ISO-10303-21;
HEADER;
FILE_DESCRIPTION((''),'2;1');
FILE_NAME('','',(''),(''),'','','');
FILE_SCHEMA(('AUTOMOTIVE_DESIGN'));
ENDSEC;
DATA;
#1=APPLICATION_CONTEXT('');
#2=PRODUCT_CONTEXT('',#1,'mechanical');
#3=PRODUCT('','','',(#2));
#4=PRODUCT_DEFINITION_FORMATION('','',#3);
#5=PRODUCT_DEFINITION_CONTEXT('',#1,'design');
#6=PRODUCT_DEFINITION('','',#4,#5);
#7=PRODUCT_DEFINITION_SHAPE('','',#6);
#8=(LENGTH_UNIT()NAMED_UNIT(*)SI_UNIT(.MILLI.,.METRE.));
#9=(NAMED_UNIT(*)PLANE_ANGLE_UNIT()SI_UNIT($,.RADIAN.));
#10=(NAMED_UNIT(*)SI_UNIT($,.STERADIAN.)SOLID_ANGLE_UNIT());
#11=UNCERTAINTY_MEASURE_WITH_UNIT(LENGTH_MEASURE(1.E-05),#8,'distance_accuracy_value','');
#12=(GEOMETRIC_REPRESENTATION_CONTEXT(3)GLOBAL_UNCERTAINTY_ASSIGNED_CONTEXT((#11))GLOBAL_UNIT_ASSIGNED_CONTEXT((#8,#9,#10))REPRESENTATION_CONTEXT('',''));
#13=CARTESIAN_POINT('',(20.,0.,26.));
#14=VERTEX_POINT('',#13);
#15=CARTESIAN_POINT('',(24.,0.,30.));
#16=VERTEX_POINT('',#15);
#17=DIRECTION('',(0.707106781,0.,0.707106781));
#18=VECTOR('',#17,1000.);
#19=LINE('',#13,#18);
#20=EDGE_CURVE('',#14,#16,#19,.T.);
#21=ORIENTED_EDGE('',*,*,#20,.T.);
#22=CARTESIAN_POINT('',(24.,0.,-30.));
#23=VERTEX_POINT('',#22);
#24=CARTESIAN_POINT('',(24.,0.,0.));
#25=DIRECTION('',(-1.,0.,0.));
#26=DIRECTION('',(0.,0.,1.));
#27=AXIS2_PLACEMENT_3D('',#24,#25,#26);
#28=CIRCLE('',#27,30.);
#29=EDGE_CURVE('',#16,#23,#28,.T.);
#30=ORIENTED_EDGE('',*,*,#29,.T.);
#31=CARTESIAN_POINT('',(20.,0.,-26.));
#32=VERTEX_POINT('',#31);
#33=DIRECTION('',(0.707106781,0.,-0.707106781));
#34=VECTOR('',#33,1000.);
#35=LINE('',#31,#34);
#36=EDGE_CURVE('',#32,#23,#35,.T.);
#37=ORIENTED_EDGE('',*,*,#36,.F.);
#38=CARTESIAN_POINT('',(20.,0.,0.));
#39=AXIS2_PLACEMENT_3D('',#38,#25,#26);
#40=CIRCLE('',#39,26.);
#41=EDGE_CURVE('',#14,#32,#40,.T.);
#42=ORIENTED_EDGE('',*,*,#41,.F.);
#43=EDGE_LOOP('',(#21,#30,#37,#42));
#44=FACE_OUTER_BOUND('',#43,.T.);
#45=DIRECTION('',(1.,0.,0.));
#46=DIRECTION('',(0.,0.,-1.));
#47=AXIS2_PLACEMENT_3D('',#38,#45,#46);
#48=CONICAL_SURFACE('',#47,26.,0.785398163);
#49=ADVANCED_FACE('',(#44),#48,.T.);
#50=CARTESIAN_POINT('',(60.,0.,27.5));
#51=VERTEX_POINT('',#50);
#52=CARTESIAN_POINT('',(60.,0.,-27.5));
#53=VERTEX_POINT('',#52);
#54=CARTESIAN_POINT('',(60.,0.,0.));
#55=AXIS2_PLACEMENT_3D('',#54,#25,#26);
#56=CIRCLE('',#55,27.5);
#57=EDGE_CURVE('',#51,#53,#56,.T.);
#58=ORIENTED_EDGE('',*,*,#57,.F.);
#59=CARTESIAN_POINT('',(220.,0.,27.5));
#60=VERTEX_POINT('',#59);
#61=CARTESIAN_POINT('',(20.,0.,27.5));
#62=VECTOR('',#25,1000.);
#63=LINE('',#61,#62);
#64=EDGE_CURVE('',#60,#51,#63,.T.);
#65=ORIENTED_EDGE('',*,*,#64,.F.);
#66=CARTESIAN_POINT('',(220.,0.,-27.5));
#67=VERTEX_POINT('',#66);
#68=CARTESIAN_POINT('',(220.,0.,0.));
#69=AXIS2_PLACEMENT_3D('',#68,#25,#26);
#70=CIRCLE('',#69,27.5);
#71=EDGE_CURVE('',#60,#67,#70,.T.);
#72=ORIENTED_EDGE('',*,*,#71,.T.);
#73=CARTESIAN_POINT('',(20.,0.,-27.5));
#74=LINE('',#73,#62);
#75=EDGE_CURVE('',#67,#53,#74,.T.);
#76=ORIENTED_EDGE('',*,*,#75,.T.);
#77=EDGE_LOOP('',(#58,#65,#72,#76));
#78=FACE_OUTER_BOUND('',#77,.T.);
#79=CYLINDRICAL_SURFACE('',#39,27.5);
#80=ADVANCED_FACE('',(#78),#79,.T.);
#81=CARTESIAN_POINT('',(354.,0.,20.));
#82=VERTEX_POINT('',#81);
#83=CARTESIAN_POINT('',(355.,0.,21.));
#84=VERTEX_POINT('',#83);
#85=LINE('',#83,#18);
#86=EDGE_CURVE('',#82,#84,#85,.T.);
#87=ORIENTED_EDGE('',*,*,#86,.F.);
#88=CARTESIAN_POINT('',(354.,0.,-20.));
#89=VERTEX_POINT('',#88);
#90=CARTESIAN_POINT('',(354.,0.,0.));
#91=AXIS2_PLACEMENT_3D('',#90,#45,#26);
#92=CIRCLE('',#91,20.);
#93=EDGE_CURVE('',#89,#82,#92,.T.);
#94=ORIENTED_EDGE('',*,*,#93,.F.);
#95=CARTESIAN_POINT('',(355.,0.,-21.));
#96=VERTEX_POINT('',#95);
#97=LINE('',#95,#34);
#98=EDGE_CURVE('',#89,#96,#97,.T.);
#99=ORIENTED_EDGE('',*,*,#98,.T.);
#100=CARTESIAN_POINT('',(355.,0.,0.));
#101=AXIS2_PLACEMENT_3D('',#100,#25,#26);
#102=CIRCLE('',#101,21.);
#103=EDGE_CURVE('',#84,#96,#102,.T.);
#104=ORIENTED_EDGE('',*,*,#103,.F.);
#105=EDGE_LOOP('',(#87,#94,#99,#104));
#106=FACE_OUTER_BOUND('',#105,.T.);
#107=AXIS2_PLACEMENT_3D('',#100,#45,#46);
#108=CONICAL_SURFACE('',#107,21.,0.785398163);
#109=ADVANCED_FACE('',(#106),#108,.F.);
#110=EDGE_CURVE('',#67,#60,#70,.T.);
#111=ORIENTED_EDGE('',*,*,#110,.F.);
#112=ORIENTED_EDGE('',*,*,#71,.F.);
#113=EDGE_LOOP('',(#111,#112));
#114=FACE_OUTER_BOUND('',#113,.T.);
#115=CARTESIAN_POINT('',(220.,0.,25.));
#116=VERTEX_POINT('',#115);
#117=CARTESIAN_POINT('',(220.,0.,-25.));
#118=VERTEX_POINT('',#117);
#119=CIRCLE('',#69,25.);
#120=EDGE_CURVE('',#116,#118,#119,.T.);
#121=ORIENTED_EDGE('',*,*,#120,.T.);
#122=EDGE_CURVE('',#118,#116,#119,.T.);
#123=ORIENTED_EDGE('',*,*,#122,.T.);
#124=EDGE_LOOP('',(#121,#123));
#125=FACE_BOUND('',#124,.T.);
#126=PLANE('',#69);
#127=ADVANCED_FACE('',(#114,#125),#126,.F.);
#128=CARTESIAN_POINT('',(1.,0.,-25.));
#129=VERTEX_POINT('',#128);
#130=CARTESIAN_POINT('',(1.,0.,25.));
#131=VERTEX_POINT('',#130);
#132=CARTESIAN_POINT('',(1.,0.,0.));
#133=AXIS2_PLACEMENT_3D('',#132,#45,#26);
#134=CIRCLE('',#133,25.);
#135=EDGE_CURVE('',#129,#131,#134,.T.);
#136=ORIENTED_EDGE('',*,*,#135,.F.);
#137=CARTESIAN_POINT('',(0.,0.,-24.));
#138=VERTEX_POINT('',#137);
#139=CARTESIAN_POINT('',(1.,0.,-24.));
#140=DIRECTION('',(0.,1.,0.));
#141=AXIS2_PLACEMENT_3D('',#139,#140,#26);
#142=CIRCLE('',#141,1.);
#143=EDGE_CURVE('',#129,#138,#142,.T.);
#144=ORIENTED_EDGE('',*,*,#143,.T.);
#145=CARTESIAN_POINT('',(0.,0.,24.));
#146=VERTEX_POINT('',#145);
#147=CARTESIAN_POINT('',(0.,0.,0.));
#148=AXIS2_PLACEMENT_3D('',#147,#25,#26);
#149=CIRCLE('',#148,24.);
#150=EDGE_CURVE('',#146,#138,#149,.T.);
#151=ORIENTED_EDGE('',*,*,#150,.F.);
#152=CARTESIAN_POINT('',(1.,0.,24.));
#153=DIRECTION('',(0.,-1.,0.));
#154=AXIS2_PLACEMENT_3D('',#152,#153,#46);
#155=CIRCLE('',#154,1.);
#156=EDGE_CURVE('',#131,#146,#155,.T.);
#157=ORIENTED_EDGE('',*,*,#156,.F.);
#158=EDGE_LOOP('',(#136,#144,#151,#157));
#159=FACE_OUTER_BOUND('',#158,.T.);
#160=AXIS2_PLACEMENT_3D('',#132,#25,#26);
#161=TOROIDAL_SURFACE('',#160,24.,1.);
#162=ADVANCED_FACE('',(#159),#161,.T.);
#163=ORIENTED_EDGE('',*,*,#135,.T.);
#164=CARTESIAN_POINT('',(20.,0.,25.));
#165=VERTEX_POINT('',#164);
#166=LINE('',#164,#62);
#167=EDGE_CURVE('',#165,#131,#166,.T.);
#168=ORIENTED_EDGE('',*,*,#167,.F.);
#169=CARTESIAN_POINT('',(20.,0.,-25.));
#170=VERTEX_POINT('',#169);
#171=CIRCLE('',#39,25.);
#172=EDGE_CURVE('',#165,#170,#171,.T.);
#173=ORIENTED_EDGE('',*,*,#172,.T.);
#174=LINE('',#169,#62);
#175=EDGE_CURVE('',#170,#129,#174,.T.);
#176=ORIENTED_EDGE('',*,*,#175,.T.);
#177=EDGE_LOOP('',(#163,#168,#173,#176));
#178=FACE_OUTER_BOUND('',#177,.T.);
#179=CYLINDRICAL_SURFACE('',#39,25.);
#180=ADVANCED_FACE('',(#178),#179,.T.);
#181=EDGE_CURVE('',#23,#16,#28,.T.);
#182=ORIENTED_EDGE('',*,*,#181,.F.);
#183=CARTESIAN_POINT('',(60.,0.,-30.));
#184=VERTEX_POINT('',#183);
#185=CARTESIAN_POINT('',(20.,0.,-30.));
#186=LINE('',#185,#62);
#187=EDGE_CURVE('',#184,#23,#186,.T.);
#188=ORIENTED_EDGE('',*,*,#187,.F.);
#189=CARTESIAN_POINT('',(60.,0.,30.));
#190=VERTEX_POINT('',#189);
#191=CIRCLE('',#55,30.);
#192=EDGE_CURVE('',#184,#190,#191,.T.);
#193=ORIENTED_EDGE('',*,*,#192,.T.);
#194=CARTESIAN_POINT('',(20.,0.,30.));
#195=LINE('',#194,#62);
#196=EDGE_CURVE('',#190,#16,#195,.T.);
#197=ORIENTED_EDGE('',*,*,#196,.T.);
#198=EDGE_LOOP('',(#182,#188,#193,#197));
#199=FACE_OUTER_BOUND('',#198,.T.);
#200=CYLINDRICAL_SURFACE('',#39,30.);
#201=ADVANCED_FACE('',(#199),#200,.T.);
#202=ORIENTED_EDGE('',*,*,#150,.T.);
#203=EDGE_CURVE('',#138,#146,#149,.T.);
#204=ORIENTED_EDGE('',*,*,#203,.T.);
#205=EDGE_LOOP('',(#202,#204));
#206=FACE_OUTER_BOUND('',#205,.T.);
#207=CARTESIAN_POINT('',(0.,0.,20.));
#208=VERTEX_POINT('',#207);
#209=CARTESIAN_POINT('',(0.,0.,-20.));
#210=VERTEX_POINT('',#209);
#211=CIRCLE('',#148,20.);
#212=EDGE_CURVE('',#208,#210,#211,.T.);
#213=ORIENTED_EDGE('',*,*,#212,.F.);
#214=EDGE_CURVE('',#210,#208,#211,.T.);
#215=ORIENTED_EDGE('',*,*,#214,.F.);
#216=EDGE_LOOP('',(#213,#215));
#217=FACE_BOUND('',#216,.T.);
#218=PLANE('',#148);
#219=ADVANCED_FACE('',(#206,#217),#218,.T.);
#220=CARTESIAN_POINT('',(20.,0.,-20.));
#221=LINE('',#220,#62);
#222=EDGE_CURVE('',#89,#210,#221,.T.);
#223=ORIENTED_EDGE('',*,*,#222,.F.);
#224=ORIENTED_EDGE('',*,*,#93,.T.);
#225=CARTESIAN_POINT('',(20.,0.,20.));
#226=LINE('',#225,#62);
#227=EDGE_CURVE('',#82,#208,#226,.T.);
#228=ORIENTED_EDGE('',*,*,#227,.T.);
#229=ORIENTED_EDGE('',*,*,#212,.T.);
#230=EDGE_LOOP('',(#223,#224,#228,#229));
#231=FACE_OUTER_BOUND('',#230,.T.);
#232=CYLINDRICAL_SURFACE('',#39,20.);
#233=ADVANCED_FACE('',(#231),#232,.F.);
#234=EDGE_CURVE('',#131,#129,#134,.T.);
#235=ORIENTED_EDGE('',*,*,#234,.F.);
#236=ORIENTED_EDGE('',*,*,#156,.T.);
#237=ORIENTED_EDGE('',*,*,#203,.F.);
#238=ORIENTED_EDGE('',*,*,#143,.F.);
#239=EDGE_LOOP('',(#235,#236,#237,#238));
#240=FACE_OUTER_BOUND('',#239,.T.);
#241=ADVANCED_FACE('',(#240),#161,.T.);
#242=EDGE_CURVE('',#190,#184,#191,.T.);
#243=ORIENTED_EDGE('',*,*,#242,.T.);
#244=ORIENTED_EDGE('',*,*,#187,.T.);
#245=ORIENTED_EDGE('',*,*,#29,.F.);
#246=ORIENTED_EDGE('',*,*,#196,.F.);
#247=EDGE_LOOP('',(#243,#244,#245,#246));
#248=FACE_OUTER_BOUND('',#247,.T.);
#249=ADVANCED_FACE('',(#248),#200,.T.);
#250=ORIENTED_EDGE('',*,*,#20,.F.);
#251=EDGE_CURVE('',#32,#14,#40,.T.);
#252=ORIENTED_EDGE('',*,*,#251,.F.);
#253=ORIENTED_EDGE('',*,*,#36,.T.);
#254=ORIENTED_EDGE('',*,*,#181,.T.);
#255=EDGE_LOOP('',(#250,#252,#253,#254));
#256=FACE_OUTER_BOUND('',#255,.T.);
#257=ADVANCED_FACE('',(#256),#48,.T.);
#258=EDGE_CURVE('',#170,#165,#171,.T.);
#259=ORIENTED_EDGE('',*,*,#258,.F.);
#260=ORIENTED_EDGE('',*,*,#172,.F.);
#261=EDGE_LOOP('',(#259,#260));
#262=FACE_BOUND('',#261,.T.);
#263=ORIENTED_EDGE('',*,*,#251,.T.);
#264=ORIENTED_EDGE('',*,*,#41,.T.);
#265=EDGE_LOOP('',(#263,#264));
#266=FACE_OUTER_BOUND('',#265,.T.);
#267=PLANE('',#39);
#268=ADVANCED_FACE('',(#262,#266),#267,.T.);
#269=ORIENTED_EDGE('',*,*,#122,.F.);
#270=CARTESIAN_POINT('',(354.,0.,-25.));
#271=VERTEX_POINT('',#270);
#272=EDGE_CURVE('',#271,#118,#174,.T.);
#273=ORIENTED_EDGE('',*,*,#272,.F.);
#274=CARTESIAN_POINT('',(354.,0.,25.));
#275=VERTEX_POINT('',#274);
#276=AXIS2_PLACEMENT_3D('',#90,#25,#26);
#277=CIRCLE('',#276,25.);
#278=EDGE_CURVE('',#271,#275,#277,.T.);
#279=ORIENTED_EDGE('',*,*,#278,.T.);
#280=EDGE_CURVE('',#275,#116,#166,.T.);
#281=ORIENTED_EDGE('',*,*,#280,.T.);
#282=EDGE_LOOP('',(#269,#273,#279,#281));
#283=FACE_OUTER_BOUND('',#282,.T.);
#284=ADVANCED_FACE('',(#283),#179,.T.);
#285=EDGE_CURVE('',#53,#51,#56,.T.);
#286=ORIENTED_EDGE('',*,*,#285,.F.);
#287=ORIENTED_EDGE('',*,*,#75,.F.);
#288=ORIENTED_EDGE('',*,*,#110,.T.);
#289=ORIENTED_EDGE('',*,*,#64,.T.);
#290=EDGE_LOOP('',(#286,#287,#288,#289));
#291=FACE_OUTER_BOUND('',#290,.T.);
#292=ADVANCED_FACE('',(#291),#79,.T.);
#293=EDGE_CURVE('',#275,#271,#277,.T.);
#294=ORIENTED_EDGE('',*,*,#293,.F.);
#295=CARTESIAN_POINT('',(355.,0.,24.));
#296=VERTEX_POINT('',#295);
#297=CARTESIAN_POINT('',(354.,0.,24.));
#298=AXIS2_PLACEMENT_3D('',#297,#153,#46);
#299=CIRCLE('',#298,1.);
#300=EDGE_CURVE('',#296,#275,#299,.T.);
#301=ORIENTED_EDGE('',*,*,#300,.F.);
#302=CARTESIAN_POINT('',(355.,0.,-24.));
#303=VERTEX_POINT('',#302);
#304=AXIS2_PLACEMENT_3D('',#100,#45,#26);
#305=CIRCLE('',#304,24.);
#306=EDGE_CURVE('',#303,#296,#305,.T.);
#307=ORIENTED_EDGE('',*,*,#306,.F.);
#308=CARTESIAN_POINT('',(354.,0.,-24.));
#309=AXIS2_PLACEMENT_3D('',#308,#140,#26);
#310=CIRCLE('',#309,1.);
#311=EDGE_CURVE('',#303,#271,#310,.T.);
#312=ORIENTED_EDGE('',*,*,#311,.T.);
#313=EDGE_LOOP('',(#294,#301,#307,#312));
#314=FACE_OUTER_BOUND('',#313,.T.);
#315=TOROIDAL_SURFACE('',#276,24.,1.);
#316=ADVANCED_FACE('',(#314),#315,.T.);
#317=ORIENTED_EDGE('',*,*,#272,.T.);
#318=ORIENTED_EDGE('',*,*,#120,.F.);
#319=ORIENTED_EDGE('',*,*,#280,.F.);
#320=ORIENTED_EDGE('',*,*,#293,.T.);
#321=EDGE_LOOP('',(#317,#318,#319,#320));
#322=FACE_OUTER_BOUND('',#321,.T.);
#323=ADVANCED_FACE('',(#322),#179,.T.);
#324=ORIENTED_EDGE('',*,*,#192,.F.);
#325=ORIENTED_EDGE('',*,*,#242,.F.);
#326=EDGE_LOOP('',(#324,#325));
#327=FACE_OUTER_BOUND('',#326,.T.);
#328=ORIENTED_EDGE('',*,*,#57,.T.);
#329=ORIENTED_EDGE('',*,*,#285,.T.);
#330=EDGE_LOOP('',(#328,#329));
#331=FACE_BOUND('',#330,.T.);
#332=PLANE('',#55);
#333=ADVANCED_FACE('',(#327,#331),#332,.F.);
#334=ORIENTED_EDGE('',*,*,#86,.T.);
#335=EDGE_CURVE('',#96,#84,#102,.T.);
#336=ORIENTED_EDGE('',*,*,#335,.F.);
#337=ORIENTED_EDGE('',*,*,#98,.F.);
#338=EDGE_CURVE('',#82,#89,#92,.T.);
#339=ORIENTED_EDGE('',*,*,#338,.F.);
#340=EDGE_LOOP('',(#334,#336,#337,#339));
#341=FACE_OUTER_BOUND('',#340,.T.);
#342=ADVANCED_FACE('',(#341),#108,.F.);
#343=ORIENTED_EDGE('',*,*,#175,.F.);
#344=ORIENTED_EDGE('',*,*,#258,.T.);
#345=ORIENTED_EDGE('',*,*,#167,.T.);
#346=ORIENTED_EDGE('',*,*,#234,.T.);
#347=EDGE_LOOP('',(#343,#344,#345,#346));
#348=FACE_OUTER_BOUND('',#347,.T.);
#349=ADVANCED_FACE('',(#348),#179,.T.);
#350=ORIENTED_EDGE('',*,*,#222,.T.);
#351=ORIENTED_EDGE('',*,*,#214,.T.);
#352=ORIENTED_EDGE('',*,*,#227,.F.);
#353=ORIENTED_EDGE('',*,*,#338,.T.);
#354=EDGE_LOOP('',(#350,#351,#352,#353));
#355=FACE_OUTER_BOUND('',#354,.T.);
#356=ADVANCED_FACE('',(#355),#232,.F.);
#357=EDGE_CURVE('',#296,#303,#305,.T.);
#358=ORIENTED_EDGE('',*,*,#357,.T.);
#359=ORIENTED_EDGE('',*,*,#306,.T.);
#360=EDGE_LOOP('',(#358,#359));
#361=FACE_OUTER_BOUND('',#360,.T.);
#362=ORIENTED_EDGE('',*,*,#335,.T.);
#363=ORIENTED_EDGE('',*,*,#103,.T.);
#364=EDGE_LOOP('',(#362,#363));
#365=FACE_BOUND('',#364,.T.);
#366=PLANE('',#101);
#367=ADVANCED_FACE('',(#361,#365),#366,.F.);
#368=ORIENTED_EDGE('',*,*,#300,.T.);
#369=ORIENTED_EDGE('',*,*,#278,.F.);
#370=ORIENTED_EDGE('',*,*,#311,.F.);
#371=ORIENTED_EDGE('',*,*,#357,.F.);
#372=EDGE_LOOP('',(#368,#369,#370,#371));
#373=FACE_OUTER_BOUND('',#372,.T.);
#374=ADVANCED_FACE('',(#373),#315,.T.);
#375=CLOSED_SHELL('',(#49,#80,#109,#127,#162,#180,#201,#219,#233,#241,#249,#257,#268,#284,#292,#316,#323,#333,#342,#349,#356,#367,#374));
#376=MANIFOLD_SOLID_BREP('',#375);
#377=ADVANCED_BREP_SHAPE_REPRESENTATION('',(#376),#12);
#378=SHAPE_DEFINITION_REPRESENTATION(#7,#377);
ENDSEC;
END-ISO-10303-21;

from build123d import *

# Parameters (mm, degrees)
FILLET1_R     = 1
CHAMFER1_SIZE = 1


with BuildPart() as part:
    # Sketch 1 → Revolve3 (revolve)
    with BuildSketch(Plane(origin=(0, 0, 0), x_dir=(1, 0, 0), z_dir=(0, 1, 0)), mode=Mode.PRIVATE) as revolve3_sk:
        Polygon((24, 30), (20, 26), (20, 25), (0, 25), (0, 20), (355, 20), (355, 25), (220, 25), (220, 27.5), (60, 27.5), (60, 30), align=None)
    revolve(revolve3_sk.sketch.rotate(Axis((20, 0, 0), (1, 0, 0)), 180), axis=Axis((20, 0, 0), (1, 0, 0)))

    # Fillet1
    fillet1_edges = [part.edges().sort_by_distance(p)[0] for p in [
        (355, 0, -25),
        (0, 0, -25),
    ]]
    fillet(fillet1_edges, radius=FILLET1_R)

    # Chamfer1
    chamfer1_edges = [part.edges().sort_by_distance(p)[0] for p in [
        (355, 0, -20),
    ]]
    chamfer(chamfer1_edges, length=CHAMFER1_SIZE)


solid = part.part
